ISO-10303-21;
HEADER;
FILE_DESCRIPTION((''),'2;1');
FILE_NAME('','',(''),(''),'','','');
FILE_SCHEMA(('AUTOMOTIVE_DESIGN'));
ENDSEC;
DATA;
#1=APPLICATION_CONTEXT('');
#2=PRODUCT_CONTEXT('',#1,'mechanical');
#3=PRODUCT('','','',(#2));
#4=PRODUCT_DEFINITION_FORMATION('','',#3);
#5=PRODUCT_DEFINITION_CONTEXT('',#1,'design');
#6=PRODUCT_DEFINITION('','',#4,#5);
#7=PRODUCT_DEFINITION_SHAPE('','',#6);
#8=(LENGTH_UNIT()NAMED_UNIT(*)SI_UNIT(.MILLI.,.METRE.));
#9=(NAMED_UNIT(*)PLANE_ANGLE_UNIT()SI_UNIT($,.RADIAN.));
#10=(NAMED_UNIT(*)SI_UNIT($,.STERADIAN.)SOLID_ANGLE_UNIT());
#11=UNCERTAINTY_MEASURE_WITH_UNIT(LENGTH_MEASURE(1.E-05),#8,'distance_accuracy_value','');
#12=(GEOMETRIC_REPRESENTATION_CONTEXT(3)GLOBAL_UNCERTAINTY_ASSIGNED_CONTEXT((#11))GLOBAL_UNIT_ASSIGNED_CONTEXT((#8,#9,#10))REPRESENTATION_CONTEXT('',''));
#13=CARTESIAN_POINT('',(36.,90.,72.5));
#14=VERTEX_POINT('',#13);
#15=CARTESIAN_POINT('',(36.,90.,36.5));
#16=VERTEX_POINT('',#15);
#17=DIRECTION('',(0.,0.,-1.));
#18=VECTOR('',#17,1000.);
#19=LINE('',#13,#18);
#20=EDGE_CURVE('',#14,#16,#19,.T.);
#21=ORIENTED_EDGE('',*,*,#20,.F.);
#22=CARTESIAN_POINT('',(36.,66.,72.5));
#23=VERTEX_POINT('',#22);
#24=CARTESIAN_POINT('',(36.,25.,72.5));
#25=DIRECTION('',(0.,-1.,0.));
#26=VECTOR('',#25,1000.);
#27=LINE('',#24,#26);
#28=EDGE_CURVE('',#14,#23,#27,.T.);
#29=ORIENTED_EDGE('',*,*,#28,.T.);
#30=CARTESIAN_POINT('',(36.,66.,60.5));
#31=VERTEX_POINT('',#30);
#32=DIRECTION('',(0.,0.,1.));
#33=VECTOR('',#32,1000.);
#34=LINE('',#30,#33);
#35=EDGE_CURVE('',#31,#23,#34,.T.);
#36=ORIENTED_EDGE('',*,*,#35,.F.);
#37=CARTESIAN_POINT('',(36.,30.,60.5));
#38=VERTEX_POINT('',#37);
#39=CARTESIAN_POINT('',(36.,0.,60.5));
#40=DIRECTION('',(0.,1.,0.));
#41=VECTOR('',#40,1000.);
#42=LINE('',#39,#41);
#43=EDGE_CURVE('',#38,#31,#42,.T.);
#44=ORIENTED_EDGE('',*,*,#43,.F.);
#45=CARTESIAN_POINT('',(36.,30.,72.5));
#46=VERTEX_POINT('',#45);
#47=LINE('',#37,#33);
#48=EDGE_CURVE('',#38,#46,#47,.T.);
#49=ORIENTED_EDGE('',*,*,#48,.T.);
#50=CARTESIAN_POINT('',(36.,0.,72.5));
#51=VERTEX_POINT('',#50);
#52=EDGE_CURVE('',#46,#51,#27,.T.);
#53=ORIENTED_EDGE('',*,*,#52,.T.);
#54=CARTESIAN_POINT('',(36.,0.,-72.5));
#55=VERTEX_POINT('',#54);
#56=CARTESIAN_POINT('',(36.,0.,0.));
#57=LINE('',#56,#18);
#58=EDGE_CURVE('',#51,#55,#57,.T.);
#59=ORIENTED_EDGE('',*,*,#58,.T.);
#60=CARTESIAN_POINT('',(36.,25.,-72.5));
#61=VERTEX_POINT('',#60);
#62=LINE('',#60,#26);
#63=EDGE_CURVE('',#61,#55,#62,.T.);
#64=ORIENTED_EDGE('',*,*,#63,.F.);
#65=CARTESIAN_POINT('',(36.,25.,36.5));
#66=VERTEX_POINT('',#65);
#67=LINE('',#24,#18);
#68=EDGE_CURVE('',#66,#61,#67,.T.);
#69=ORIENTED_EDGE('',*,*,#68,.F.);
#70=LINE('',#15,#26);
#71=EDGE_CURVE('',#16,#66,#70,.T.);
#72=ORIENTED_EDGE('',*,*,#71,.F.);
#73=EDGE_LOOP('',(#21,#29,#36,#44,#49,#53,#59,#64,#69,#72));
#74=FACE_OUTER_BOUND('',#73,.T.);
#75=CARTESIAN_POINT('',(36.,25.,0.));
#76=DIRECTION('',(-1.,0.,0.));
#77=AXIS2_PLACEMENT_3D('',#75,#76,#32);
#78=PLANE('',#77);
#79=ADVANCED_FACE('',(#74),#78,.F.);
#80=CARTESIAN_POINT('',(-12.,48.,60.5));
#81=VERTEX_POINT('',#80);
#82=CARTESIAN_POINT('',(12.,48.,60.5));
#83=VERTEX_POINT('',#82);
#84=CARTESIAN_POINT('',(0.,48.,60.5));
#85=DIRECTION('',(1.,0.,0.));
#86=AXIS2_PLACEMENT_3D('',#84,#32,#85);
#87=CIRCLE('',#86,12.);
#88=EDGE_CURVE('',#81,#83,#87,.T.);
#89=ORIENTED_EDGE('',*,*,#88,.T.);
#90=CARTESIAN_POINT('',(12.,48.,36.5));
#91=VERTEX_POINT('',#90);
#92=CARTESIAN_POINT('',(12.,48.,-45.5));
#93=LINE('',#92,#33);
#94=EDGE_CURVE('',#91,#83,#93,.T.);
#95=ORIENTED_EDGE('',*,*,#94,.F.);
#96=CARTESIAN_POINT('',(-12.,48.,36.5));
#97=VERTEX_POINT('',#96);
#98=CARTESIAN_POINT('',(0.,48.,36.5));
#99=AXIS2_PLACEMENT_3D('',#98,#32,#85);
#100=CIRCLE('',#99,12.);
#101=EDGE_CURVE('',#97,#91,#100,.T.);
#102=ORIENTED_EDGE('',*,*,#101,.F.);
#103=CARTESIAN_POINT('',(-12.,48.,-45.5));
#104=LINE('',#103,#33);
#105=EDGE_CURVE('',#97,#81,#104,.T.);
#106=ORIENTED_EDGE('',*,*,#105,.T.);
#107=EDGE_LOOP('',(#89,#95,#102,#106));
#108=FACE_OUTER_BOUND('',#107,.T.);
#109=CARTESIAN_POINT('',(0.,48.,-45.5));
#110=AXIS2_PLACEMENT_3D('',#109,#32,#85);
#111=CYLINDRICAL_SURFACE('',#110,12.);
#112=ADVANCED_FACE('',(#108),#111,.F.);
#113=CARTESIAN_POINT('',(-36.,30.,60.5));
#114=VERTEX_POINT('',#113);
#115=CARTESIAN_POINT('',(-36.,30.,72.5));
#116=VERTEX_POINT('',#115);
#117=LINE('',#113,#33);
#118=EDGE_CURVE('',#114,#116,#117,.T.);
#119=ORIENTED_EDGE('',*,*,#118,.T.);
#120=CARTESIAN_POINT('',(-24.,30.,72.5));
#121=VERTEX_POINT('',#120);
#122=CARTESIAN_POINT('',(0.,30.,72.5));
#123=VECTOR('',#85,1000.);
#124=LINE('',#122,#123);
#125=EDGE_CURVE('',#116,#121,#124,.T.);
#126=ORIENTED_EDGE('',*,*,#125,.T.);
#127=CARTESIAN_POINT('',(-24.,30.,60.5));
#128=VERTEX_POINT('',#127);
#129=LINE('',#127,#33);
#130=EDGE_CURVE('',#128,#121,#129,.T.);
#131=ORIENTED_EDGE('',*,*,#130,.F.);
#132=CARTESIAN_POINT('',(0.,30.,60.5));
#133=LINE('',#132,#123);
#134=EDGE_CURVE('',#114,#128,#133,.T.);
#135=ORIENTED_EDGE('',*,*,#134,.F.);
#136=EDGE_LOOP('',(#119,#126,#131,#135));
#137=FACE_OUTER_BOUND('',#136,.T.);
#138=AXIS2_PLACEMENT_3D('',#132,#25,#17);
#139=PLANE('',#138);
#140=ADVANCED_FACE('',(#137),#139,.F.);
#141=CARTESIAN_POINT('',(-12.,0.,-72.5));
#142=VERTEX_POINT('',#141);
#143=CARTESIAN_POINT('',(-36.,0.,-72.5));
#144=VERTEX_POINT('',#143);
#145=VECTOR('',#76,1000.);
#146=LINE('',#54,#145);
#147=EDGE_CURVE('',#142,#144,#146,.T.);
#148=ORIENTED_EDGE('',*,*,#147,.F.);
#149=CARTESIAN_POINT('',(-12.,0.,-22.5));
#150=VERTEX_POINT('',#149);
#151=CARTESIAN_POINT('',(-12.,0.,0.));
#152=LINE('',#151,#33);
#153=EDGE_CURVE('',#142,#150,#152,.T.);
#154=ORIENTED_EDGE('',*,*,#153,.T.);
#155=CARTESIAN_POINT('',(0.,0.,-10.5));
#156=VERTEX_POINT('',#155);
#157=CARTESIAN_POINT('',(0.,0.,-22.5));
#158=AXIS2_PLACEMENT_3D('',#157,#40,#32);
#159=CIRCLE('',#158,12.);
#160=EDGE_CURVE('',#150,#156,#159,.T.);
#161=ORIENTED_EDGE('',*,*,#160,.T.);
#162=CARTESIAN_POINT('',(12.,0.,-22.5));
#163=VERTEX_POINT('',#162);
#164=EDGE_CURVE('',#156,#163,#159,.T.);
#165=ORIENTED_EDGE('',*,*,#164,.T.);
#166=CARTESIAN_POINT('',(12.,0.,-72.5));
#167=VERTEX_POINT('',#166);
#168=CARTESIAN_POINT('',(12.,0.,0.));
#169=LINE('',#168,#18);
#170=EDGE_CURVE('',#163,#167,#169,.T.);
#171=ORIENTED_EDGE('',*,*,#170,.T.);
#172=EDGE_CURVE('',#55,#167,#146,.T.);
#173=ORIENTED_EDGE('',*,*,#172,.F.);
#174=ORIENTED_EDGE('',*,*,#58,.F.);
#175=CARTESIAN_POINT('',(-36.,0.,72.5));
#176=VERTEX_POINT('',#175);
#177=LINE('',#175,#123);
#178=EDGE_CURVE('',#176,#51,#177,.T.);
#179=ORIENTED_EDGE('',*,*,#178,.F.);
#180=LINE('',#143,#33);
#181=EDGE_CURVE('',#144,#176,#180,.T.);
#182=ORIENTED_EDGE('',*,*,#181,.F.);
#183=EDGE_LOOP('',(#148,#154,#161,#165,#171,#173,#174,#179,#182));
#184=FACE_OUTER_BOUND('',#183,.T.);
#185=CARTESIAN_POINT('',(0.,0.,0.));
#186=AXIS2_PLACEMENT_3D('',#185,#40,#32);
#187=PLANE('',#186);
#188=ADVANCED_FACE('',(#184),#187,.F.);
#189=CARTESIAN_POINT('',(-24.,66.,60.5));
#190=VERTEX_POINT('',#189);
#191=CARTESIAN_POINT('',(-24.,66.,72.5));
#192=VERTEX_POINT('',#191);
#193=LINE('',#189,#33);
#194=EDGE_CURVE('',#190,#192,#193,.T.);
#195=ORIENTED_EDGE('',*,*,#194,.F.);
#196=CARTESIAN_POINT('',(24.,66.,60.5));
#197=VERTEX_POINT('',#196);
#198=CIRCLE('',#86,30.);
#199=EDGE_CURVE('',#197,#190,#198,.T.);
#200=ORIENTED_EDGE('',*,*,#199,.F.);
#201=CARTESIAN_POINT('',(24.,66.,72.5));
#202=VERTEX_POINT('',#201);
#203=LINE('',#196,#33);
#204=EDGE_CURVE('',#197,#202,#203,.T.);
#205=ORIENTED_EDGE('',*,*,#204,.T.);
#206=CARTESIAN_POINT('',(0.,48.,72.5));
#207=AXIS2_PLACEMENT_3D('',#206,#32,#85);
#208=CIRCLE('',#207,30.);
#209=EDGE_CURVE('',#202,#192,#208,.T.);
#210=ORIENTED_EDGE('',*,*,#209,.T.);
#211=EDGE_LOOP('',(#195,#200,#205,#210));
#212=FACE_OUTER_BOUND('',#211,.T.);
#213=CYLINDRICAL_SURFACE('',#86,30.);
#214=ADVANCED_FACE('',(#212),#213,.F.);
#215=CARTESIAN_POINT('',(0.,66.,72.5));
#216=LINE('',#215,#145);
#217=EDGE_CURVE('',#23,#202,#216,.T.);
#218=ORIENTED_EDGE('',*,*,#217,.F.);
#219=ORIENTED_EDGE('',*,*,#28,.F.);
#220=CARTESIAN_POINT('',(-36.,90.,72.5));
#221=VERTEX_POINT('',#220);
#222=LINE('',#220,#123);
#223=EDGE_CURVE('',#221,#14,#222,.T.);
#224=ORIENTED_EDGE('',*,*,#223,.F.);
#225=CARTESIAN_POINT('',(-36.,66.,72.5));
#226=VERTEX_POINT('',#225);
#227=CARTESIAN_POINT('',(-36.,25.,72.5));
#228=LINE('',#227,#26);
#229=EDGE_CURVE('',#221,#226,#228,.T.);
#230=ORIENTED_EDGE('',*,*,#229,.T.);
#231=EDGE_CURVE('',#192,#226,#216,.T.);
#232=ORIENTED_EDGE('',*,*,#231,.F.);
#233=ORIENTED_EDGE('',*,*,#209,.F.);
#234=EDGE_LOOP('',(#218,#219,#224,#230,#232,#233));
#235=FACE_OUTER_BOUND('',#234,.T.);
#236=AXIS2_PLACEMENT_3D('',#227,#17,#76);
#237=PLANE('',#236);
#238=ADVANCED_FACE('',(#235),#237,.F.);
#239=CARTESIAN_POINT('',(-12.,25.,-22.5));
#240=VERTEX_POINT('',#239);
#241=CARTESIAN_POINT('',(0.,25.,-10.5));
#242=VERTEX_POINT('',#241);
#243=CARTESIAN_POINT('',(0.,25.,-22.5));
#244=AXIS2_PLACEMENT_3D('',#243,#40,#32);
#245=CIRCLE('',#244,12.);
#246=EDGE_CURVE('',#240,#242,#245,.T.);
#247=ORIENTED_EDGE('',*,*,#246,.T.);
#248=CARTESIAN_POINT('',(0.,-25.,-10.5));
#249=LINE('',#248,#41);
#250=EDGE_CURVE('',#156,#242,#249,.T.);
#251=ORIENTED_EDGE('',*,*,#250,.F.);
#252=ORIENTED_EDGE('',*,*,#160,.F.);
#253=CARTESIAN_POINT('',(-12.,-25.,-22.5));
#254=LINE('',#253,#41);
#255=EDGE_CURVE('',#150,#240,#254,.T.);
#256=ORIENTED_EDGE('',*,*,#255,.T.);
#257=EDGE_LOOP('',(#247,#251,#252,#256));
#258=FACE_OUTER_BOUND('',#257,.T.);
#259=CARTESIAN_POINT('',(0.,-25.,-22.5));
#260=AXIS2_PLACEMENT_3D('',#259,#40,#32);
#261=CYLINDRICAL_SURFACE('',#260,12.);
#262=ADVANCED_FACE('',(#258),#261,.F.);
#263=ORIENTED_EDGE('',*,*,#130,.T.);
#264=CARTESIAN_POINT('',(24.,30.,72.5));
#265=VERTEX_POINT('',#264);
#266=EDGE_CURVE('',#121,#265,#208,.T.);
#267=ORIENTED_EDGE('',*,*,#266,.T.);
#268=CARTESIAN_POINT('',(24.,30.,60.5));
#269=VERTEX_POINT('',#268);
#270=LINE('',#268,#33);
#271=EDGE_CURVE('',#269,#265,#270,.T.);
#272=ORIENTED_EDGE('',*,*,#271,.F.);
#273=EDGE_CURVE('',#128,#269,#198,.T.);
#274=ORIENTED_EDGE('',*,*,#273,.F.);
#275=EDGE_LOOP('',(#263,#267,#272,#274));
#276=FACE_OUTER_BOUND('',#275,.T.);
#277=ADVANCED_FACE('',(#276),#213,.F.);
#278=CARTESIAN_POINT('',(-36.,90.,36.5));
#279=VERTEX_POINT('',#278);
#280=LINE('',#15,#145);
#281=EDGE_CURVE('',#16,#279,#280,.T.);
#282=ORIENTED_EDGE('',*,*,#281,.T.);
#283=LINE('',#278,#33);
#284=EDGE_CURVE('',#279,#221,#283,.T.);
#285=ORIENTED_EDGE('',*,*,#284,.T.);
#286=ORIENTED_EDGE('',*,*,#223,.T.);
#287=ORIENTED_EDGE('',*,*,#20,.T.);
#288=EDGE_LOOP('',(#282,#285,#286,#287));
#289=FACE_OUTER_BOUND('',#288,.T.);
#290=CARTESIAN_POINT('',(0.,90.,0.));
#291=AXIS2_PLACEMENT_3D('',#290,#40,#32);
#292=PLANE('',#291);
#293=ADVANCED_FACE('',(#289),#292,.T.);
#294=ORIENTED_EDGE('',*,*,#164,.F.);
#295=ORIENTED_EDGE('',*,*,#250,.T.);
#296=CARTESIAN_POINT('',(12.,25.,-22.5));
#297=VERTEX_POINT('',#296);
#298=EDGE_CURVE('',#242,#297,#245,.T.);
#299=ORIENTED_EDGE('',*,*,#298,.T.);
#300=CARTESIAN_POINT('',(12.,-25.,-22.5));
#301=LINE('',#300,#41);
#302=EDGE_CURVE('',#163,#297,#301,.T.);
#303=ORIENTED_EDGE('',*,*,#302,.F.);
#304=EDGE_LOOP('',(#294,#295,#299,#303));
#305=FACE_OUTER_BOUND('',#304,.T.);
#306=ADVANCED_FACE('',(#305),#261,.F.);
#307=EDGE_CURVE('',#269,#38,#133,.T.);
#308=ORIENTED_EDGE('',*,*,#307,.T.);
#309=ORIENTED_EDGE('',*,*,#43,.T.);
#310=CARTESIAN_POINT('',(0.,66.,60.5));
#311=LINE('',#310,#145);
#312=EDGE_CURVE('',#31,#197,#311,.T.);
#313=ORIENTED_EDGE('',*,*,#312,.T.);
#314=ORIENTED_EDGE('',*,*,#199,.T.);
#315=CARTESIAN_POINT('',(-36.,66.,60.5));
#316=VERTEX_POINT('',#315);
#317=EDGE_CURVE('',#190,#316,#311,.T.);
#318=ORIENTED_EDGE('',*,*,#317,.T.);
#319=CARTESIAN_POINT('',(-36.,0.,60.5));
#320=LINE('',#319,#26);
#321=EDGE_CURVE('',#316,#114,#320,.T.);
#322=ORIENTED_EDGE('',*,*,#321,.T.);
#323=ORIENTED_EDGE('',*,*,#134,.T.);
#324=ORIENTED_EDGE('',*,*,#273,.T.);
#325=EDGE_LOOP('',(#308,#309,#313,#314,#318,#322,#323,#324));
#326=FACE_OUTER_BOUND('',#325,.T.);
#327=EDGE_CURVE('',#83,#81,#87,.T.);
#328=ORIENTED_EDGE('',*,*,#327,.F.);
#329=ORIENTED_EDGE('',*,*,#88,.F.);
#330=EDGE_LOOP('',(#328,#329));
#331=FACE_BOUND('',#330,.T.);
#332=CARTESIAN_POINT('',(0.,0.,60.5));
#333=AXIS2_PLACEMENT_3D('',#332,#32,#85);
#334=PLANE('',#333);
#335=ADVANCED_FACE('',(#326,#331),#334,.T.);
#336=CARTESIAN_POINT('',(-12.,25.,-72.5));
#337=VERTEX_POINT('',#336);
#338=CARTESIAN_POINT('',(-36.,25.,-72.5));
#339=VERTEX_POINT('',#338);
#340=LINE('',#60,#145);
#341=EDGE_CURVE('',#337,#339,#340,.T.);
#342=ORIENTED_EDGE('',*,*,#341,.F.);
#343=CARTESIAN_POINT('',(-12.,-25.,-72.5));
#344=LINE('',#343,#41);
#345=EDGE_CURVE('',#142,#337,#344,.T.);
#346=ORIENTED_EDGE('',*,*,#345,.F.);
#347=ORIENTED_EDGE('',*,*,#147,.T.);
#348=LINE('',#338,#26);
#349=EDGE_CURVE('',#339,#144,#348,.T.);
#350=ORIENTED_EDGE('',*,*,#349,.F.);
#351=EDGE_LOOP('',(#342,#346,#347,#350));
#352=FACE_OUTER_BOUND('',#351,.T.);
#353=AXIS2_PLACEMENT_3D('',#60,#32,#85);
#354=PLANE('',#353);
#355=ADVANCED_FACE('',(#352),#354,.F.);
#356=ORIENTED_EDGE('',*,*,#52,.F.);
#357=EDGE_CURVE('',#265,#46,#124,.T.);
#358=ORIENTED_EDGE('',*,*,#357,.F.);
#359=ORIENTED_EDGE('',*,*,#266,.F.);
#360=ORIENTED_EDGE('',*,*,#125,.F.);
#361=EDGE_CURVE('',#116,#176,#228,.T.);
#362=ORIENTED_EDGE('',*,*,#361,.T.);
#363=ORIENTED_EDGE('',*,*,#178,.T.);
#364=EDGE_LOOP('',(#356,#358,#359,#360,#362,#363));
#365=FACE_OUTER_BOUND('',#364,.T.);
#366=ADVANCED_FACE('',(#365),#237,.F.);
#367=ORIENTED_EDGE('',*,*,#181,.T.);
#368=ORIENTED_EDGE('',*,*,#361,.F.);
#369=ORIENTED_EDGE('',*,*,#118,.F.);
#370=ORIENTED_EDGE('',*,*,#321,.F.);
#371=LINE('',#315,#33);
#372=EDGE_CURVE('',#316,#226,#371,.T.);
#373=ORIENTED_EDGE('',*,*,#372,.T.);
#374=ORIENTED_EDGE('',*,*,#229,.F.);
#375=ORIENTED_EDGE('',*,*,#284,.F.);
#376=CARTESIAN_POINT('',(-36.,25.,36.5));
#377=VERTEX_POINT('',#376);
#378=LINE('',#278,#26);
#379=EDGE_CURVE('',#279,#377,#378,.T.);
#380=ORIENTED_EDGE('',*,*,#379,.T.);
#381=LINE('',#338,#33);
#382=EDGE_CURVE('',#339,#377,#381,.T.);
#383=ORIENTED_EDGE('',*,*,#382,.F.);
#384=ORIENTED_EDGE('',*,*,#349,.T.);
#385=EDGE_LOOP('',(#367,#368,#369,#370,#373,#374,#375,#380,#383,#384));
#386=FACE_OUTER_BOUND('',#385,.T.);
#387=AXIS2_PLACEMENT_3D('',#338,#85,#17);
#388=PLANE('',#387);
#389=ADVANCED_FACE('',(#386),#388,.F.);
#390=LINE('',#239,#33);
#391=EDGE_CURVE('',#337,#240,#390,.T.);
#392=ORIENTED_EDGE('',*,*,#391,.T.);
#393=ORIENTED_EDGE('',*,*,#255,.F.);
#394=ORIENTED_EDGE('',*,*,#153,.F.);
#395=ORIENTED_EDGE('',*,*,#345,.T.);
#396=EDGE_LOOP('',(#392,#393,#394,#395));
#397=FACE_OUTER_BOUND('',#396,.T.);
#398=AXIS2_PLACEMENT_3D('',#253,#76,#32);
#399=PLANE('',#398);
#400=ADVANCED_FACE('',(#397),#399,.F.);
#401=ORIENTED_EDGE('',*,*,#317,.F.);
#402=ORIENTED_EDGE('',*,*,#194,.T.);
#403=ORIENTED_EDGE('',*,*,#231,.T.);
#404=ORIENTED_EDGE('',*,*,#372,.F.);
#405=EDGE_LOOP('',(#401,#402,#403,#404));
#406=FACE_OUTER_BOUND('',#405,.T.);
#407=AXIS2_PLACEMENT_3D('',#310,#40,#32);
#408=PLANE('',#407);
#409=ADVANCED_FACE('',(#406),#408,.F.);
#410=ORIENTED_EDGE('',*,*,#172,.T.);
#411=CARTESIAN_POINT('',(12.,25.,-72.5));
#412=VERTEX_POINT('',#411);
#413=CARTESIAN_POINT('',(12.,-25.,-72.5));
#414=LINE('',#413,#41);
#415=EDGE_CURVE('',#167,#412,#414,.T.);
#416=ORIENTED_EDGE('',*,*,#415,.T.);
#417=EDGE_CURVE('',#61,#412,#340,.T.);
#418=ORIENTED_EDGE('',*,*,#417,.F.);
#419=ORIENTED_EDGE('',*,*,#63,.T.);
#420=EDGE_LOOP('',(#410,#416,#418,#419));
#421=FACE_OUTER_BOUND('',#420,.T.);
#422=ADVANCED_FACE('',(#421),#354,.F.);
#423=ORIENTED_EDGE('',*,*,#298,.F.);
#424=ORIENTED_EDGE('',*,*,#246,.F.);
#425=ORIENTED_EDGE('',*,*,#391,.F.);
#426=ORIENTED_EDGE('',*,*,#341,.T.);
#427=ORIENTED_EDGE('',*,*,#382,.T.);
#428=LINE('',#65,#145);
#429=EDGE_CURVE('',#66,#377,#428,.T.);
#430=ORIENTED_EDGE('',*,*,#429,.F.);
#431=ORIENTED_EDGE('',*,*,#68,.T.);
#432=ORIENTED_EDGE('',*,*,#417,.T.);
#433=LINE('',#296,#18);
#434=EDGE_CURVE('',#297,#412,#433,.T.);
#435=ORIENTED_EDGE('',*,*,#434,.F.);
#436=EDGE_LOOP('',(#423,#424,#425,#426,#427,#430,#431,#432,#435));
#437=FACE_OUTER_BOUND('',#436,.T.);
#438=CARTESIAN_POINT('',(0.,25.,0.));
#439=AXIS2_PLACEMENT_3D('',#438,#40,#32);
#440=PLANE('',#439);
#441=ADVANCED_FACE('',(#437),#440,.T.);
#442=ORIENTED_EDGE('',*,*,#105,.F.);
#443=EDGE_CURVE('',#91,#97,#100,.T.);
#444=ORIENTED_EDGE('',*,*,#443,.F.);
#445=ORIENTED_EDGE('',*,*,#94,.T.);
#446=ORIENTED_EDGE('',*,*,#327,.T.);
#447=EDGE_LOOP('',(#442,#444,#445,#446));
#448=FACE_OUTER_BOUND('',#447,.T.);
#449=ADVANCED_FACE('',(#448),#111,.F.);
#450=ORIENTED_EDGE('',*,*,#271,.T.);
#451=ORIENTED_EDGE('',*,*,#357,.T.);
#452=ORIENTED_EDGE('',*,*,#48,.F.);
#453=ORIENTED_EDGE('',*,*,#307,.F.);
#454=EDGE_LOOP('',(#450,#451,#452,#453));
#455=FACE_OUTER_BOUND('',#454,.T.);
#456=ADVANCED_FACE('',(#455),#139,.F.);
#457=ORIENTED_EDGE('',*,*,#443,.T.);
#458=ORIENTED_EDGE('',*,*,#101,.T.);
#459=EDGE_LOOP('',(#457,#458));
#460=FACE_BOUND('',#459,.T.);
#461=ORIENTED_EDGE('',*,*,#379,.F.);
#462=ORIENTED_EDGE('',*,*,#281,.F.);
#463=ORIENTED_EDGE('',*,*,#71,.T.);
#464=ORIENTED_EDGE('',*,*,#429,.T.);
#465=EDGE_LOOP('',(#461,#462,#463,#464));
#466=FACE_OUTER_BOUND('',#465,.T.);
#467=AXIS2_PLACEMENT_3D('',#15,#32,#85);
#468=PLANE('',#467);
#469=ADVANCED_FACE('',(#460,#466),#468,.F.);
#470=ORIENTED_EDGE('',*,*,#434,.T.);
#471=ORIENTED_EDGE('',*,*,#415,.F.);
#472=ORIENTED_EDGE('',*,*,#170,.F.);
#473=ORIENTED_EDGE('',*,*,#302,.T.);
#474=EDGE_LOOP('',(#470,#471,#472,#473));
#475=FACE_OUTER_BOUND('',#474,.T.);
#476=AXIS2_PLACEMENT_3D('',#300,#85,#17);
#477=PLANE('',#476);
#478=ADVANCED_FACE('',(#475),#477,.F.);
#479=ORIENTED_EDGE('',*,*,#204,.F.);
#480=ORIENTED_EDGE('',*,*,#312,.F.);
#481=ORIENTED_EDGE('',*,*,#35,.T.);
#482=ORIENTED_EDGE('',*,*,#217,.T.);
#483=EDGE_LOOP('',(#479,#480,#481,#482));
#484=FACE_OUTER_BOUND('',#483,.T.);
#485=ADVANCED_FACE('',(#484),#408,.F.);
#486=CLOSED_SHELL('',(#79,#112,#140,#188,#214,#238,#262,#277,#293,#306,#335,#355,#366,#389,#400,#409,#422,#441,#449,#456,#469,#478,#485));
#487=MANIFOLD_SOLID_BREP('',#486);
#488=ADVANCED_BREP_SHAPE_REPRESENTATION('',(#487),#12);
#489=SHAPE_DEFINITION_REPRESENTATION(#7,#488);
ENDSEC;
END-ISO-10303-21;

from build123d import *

# Parameters (mm, degrees)
BASE_PLATE_DEPTH       = 25
BASE_SLOT_DEPTH        = 50
UPRIGHT_BLOCK_SKETCH_W = 72
UPRIGHT_BLOCK_SKETCH_H = 36
UPRIGHT_BLOCK_DEPTH    = 65
BEARING_SEAT_CUT_DEPTH = 12
THROUGH_BORE_SKETCH_R  = 12
THROUGH_BORE_DEPTH     = 106


with BuildPart() as part:
    # Base Plate Sketch → Base Plate (new body)
    with BuildSketch(Plane(origin=(0, 0, 0), x_dir=(1, 0, 0), z_dir=(0, 1, 0))):
        Polygon((36, 0), (36, 72.5), (-36, 72.5), (-36, -72.5), (36, -72.5), align=None)
    extrude(amount=BASE_PLATE_DEPTH)

    # Base Slot Sketch → Base Slot (cut)
    with BuildSketch(Plane(origin=(0, 25, 0), x_dir=(1, 0, 0), z_dir=(0, 1, 0))):
        with BuildLine():
            Line((12, 22.5), (12, 72.5))
            Line((12, 72.5), (-12, 72.5))
            Line((-12, 72.5), (-12, 22.5))
            ThreePointArc((-12, 22.5), (0, 10.5), (12, 22.5))
        make_face()
    extrude(amount=-BASE_SLOT_DEPTH, mode=Mode.SUBTRACT)

    # Upright Block Sketch → Upright Block (add)
    with BuildSketch(Plane(origin=(0, 25, 0), x_dir=(1, 0, 0), z_dir=(0, 1, 0))):
        with Locations((0, -54.5)):
            Rectangle(UPRIGHT_BLOCK_SKETCH_W, UPRIGHT_BLOCK_SKETCH_H)
    extrude(amount=UPRIGHT_BLOCK_DEPTH)

    # Bearing Seat Sketch → Bearing Seat Cut (cut)
    with BuildSketch(Plane.XY.offset(72.5)):
        with BuildLine():
            Line((-36, 66), (-36, 30))
            Line((-36, 30), (-24, 30))
            ThreePointArc((-24, 30), (0, 18), (24, 30))
            Line((24, 30), (36, 30))
            Line((36, 30), (36, 66))
            Line((36, 66), (24, 66))
            ThreePointArc((24, 66), (0, 78), (-24, 66))
            Line((-24, 66), (-36, 66))
        make_face()
    extrude(amount=-BEARING_SEAT_CUT_DEPTH, mode=Mode.SUBTRACT)

    # Through Bore Sketch → Through Bore (cut)
    with BuildSketch(Plane.XY.offset(60.5)):
        with Locations((0, 48)):
            Circle(THROUGH_BORE_SKETCH_R)
    extrude(amount=-THROUGH_BORE_DEPTH, mode=Mode.SUBTRACT)


solid = part.part
